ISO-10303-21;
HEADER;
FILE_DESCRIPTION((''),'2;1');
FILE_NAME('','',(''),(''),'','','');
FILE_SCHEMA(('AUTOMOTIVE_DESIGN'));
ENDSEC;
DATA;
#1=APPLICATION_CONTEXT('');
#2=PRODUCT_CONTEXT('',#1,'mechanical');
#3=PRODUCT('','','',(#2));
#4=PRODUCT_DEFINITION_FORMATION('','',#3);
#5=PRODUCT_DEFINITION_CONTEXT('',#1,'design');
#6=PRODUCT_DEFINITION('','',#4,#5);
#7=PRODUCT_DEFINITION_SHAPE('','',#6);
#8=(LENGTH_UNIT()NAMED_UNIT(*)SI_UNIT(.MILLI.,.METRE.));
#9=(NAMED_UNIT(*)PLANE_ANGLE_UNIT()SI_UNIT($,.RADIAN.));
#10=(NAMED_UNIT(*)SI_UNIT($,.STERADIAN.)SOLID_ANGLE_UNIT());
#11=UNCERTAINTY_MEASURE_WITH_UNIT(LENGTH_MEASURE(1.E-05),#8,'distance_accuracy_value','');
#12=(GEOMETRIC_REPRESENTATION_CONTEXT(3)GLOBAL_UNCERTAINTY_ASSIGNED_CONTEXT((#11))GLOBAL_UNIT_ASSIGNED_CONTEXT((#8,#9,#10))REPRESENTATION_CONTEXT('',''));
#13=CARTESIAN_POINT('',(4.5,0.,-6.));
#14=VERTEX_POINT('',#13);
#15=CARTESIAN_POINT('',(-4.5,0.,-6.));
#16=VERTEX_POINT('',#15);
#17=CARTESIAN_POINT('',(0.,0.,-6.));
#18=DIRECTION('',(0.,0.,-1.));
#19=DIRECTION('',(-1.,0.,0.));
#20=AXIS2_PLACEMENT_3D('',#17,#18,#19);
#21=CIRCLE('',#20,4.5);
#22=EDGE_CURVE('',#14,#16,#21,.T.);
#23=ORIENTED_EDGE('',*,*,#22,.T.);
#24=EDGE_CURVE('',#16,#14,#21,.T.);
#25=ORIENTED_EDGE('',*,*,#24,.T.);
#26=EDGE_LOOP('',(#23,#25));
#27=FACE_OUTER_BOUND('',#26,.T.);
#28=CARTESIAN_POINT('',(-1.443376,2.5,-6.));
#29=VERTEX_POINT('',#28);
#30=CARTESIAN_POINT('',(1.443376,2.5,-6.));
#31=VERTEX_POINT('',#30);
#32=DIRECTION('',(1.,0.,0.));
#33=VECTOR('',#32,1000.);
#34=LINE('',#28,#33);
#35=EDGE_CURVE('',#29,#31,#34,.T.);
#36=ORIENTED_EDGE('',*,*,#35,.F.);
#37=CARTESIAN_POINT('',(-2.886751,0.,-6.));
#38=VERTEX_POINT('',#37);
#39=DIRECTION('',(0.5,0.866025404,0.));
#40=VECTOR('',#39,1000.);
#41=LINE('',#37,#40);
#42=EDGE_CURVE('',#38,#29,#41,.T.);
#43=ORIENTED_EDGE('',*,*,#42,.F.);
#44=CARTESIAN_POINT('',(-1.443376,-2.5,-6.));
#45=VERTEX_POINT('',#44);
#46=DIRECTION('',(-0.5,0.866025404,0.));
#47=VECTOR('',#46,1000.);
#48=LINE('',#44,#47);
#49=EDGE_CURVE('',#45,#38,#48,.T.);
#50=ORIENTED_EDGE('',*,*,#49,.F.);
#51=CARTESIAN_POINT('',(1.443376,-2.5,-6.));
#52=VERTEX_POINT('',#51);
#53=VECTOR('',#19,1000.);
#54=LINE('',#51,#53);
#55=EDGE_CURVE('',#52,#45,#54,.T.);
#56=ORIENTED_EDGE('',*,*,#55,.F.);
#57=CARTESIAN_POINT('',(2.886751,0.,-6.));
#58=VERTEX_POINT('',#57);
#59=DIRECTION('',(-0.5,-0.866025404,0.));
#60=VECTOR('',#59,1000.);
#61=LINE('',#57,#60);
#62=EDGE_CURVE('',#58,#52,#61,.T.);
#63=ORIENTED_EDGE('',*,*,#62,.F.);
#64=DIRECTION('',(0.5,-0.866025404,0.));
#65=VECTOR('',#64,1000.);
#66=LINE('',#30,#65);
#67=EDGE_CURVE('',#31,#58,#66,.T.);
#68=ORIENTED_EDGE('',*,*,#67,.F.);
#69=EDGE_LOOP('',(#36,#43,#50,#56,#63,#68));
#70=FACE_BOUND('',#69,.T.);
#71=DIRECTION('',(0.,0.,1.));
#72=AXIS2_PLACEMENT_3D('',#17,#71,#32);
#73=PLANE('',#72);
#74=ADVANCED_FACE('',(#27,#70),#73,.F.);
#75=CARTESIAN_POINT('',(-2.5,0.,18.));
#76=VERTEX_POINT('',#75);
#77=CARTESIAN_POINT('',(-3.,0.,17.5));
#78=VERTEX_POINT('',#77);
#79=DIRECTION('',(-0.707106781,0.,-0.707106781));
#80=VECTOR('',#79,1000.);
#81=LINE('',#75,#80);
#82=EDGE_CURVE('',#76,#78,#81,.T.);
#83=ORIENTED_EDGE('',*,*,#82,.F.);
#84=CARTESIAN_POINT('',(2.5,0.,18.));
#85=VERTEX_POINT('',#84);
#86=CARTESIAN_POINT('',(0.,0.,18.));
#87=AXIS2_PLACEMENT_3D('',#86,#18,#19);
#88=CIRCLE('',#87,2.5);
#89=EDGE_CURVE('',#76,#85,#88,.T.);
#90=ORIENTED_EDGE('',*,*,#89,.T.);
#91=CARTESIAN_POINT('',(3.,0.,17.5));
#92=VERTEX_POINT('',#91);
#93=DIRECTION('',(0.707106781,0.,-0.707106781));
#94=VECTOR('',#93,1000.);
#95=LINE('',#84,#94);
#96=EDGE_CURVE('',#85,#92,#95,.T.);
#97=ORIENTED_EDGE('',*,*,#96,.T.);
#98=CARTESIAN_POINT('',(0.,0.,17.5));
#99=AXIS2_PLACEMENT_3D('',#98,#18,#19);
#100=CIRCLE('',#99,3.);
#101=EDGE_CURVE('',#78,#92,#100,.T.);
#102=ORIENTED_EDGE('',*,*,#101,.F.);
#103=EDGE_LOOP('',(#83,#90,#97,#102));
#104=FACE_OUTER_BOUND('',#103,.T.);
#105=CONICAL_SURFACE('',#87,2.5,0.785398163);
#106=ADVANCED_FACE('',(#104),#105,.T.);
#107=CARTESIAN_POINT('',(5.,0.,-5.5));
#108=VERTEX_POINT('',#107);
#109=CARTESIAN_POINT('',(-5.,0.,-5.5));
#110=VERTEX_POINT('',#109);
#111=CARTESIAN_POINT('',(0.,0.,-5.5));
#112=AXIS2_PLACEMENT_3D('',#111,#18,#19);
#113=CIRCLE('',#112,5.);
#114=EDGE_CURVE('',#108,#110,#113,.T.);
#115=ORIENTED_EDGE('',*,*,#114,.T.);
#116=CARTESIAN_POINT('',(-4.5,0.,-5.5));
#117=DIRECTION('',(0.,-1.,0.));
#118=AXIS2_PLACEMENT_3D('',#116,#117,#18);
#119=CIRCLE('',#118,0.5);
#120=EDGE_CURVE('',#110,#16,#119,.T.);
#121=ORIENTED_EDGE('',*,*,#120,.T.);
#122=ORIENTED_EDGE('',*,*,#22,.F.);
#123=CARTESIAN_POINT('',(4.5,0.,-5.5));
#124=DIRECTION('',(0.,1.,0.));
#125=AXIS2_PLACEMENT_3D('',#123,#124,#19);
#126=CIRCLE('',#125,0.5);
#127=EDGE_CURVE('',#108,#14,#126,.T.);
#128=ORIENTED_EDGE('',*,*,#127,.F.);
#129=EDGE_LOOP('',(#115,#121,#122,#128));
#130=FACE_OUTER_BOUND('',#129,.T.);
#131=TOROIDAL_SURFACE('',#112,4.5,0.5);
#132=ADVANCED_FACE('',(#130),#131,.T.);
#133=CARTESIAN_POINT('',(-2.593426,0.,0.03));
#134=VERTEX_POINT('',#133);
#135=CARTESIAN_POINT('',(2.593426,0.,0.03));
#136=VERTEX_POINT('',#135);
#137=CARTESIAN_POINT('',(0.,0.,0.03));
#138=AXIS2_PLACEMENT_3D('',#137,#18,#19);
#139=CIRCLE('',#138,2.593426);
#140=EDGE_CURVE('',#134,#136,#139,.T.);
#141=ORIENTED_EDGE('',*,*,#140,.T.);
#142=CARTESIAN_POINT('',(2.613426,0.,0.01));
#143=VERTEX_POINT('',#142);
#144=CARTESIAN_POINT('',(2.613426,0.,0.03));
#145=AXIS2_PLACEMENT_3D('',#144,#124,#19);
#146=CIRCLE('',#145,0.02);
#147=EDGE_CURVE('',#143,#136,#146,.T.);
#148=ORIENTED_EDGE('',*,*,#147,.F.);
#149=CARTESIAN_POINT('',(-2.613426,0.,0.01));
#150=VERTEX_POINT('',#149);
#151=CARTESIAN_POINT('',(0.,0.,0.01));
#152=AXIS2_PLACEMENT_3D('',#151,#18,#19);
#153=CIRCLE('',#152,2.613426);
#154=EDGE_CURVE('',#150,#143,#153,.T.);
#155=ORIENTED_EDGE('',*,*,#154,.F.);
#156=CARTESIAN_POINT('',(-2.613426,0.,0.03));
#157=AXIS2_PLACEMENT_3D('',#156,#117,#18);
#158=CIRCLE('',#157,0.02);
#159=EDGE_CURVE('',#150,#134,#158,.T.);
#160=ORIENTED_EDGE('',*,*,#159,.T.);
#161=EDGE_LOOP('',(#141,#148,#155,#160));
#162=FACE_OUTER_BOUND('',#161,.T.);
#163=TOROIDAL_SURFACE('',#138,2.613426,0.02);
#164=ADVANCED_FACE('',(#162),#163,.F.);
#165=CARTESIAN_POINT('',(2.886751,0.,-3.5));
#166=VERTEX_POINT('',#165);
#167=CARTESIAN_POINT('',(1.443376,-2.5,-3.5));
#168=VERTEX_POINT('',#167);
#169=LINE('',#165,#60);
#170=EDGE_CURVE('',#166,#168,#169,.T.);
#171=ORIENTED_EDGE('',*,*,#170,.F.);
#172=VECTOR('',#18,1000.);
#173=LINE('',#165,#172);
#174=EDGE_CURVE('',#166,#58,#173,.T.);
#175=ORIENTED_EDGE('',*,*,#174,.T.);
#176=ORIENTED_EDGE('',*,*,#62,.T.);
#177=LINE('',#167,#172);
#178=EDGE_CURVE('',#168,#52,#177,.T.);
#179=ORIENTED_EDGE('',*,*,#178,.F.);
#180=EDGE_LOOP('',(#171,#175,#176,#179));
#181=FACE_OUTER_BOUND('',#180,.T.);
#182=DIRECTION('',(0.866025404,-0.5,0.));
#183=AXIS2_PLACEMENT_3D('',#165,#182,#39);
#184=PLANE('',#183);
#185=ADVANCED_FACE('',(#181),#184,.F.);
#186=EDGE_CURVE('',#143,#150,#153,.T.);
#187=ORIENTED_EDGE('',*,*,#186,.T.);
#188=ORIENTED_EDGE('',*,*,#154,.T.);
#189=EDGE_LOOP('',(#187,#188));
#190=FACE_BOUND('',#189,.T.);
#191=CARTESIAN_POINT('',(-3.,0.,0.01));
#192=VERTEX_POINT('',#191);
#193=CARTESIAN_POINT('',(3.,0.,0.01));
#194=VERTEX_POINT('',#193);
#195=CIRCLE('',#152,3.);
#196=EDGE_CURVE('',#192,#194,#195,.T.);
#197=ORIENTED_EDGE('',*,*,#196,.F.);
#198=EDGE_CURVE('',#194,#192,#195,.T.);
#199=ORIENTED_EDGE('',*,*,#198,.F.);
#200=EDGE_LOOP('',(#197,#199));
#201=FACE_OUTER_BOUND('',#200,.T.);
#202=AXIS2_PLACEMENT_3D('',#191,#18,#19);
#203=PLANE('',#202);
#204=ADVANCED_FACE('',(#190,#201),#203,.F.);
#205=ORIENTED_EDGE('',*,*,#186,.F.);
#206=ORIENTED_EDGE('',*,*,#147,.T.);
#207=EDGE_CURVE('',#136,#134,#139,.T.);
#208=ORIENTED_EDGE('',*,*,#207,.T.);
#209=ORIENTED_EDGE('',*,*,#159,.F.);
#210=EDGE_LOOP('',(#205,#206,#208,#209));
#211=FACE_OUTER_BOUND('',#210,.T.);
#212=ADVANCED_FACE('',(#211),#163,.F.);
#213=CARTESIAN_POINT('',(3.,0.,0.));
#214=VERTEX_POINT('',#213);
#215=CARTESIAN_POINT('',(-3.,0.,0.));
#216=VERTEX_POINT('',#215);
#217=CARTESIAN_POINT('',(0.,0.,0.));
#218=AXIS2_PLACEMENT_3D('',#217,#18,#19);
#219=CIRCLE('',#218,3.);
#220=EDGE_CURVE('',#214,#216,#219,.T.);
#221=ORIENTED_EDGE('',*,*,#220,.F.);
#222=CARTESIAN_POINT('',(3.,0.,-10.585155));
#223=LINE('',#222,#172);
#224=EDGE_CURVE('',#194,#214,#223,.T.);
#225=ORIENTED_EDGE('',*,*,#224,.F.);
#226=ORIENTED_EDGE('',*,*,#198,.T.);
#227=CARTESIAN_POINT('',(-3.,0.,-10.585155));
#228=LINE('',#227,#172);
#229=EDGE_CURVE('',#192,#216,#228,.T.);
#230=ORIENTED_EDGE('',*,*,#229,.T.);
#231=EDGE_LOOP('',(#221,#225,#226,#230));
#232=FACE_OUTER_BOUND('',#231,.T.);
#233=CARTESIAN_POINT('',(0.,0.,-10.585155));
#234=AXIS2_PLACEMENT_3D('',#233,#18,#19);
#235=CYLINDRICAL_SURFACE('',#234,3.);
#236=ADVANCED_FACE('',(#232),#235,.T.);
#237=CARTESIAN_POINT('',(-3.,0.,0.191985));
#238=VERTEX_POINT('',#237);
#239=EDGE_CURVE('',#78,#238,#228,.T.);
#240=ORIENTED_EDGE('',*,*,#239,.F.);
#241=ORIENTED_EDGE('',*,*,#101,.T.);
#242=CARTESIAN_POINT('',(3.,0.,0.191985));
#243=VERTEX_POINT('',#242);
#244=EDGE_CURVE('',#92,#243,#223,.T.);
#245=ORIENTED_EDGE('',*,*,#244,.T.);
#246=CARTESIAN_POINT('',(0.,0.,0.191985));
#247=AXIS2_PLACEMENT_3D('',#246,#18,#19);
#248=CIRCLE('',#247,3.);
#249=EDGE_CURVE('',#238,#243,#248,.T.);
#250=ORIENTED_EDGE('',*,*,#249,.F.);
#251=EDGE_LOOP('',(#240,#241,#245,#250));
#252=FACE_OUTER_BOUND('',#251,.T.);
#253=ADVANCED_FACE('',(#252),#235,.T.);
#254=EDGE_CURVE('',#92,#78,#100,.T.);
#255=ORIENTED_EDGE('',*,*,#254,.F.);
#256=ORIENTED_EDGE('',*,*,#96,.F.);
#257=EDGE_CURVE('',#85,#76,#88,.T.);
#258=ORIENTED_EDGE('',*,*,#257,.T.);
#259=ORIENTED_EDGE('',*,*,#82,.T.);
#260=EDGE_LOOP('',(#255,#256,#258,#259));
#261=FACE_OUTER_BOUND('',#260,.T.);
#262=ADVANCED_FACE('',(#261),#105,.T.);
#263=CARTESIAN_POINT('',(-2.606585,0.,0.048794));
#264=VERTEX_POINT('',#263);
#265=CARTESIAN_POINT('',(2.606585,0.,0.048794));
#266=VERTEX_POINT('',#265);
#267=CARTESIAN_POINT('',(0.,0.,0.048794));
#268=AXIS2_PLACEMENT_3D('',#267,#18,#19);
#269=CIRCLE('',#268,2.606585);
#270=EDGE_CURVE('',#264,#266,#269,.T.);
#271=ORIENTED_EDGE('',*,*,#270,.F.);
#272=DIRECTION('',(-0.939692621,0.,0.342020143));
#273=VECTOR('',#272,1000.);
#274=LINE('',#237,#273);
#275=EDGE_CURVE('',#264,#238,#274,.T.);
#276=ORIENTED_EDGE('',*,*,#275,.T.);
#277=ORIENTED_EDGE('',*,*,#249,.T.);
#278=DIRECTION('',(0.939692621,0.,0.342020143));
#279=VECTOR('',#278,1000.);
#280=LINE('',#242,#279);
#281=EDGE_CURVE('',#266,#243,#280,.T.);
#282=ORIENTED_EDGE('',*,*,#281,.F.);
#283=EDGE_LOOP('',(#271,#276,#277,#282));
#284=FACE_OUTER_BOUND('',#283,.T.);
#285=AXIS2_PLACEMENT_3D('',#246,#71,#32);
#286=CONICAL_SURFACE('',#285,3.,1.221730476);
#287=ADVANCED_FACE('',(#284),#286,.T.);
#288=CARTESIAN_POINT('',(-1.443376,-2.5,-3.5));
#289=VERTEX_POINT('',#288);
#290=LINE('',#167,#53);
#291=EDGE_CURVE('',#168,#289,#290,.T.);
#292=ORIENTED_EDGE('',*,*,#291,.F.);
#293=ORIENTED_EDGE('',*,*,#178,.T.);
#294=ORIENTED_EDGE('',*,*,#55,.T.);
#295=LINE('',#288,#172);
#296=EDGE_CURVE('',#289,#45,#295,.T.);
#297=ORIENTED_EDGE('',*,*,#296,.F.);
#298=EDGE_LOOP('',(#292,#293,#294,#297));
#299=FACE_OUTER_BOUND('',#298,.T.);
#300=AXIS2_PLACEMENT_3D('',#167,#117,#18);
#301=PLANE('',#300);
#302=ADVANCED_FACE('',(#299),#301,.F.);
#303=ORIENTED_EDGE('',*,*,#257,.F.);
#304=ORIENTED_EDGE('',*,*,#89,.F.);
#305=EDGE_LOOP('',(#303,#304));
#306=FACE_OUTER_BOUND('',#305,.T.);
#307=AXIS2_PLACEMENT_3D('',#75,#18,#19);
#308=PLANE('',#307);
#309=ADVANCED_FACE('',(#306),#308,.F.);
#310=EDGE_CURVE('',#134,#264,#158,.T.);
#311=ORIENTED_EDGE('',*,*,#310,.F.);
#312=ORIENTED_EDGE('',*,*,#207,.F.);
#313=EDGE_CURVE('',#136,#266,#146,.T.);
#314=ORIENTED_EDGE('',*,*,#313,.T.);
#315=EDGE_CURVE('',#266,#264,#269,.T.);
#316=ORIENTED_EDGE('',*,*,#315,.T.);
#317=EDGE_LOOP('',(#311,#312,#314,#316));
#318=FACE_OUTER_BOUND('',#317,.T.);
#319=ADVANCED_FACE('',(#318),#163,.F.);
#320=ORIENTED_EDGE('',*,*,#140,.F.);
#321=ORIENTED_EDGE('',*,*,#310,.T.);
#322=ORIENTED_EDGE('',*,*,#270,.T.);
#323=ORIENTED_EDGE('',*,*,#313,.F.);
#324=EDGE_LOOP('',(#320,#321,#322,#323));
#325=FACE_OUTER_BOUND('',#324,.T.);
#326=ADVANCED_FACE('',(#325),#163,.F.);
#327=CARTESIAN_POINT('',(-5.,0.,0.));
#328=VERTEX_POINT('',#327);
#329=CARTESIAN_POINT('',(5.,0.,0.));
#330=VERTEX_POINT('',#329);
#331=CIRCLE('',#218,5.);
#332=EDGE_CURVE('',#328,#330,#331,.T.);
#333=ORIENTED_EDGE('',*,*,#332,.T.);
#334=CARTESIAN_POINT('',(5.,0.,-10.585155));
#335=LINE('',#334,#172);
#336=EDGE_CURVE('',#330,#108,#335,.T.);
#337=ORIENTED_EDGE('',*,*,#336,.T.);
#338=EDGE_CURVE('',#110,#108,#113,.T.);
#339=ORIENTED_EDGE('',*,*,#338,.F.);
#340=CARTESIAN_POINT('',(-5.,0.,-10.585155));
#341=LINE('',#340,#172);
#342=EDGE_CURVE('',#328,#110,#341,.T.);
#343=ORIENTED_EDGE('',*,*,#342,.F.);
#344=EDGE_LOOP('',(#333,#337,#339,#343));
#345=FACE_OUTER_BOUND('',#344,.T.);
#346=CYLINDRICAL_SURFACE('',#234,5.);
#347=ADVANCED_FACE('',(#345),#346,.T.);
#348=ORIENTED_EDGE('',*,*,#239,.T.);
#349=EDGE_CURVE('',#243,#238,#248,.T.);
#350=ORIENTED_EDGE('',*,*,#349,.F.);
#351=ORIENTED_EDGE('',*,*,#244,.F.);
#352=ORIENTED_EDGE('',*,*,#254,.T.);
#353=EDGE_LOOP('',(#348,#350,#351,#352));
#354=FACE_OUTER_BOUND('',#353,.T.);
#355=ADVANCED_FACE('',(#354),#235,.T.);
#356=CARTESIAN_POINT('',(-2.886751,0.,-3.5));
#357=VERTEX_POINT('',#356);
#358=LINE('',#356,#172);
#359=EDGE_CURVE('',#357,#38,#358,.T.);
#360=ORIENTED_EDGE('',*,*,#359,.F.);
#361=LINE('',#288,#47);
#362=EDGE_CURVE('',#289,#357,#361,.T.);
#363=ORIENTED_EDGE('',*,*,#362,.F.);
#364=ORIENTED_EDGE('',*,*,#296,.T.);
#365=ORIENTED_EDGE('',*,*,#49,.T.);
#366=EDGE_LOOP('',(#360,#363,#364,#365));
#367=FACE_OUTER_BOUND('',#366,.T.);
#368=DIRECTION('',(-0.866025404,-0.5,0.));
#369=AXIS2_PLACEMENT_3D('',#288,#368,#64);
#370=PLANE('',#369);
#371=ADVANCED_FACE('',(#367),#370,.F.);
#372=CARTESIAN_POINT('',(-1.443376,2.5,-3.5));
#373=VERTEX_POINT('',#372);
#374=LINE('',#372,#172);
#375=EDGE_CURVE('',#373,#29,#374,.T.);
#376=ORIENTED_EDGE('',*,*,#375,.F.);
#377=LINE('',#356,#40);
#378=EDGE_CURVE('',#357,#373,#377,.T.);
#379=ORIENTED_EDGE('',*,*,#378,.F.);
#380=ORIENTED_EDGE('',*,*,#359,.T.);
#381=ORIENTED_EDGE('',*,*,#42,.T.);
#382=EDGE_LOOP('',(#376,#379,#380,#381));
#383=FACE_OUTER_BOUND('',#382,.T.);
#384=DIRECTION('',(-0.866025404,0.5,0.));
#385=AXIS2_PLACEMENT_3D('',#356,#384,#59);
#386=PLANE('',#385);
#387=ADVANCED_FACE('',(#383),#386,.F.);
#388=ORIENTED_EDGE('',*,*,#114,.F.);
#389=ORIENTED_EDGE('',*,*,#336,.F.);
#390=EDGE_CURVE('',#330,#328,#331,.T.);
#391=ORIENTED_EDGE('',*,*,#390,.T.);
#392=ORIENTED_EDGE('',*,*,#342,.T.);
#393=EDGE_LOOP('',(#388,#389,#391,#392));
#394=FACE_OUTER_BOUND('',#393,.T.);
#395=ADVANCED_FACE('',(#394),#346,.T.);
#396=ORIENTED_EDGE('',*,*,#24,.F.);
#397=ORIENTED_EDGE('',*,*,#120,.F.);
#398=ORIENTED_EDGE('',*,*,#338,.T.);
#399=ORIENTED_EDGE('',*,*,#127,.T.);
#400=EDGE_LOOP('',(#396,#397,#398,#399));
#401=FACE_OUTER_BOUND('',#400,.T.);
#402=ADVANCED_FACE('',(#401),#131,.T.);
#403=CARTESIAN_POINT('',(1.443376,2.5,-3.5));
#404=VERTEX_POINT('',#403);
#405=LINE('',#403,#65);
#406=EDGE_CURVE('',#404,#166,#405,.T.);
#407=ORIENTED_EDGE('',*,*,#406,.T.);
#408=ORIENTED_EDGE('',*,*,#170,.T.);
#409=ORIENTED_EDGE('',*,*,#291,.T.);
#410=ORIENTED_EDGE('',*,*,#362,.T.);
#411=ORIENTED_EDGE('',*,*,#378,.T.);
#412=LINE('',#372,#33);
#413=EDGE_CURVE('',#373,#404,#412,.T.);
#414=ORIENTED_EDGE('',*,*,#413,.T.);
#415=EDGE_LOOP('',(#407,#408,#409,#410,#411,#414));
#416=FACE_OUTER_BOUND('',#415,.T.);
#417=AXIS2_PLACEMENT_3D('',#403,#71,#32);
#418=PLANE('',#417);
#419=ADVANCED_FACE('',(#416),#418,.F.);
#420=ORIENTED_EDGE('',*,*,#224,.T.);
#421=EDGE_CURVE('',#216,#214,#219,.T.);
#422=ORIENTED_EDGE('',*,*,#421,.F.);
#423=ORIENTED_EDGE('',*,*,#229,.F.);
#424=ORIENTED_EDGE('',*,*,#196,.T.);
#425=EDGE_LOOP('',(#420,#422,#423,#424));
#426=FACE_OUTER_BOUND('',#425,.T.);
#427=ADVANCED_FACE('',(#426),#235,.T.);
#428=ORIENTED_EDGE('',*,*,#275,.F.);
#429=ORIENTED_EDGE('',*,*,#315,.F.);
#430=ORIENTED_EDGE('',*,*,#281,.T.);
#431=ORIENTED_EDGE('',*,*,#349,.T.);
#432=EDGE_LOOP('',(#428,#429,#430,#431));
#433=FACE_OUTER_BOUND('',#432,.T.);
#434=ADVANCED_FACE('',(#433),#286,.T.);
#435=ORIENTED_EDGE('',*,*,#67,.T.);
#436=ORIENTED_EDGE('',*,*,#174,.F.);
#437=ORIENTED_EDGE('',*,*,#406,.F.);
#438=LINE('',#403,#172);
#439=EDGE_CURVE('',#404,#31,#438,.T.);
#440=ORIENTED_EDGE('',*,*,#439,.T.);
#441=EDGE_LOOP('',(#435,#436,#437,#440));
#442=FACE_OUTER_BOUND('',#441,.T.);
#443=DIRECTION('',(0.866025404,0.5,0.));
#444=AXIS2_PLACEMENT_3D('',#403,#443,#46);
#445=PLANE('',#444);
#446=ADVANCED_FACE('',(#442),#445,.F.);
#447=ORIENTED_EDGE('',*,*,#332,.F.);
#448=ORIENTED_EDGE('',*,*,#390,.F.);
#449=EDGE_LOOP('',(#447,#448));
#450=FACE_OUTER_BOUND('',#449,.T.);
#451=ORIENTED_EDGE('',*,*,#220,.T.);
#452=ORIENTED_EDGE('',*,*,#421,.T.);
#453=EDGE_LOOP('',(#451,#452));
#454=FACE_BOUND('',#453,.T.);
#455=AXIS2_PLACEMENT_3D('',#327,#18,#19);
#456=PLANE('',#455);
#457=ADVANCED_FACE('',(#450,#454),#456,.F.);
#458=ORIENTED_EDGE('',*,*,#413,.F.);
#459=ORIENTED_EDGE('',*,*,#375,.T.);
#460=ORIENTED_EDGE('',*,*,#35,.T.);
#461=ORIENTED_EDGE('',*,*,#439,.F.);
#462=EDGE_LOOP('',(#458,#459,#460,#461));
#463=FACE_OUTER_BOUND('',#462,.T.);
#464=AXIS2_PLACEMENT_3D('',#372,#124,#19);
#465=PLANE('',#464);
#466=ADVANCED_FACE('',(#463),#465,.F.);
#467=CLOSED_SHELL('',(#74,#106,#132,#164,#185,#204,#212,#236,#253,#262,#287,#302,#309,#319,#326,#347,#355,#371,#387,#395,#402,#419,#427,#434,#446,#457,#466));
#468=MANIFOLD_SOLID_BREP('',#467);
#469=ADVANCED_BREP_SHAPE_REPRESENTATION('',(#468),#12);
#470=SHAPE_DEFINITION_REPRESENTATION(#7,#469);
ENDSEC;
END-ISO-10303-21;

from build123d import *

# Parameters (mm, degrees)
CUT_EXTRUDE1_DEPTH = 2.5


with BuildPart() as part:
    # Logo3_bib1 → Revolve1 (revolve)
    with BuildSketch(Plane(origin=(0, 0, 0), x_dir=(-1, 0, 0), z_dir=(0, -1, 0))):
        with BuildLine():
            Line((0, -18), (0, 6))
            Line((0, 6), (4.5, 6))
            ThreePointArc((4.5, 6), (4.853553391, 5.853553391), (5, 5.5))
            Line((5, 5.5), (5, 0))
            Line((5, 0), (3, 0))
            Line((3, 0), (3, -0.01))
            Line((3, -0.01), (2.613425636, -0.01))
            ThreePointArc((2.613425636, -0.01), (2.593729481, -0.026527036), (2.606585234, -0.048793852))
            Line((2.606585234, -0.048793852), (3, -0.191985117))
            Line((3, -0.191985117), (3, -17.5))
            Line((3, -17.5), (2.5, -18))
            Line((2.5, -18), (0, -18))
        make_face()
    revolve(axis=Axis((0, 0, -10.585154653), (0, 0, 1)))

    # Logo3_bib2 → Cut-Extrude1 (cut)
    with BuildSketch(Plane(origin=(0, 0, -6), x_dir=(1, 0, 0), z_dir=(0, 0, -1))):
        Polygon((2.886751346, 0), (1.443375673, 2.5), (-1.443375673, 2.5), (-2.886751346, 0), (-1.443375673, -2.5), (1.443375673, -2.5), align=None)
    extrude(amount=-CUT_EXTRUDE1_DEPTH, mode=Mode.SUBTRACT)


solid = part.part
